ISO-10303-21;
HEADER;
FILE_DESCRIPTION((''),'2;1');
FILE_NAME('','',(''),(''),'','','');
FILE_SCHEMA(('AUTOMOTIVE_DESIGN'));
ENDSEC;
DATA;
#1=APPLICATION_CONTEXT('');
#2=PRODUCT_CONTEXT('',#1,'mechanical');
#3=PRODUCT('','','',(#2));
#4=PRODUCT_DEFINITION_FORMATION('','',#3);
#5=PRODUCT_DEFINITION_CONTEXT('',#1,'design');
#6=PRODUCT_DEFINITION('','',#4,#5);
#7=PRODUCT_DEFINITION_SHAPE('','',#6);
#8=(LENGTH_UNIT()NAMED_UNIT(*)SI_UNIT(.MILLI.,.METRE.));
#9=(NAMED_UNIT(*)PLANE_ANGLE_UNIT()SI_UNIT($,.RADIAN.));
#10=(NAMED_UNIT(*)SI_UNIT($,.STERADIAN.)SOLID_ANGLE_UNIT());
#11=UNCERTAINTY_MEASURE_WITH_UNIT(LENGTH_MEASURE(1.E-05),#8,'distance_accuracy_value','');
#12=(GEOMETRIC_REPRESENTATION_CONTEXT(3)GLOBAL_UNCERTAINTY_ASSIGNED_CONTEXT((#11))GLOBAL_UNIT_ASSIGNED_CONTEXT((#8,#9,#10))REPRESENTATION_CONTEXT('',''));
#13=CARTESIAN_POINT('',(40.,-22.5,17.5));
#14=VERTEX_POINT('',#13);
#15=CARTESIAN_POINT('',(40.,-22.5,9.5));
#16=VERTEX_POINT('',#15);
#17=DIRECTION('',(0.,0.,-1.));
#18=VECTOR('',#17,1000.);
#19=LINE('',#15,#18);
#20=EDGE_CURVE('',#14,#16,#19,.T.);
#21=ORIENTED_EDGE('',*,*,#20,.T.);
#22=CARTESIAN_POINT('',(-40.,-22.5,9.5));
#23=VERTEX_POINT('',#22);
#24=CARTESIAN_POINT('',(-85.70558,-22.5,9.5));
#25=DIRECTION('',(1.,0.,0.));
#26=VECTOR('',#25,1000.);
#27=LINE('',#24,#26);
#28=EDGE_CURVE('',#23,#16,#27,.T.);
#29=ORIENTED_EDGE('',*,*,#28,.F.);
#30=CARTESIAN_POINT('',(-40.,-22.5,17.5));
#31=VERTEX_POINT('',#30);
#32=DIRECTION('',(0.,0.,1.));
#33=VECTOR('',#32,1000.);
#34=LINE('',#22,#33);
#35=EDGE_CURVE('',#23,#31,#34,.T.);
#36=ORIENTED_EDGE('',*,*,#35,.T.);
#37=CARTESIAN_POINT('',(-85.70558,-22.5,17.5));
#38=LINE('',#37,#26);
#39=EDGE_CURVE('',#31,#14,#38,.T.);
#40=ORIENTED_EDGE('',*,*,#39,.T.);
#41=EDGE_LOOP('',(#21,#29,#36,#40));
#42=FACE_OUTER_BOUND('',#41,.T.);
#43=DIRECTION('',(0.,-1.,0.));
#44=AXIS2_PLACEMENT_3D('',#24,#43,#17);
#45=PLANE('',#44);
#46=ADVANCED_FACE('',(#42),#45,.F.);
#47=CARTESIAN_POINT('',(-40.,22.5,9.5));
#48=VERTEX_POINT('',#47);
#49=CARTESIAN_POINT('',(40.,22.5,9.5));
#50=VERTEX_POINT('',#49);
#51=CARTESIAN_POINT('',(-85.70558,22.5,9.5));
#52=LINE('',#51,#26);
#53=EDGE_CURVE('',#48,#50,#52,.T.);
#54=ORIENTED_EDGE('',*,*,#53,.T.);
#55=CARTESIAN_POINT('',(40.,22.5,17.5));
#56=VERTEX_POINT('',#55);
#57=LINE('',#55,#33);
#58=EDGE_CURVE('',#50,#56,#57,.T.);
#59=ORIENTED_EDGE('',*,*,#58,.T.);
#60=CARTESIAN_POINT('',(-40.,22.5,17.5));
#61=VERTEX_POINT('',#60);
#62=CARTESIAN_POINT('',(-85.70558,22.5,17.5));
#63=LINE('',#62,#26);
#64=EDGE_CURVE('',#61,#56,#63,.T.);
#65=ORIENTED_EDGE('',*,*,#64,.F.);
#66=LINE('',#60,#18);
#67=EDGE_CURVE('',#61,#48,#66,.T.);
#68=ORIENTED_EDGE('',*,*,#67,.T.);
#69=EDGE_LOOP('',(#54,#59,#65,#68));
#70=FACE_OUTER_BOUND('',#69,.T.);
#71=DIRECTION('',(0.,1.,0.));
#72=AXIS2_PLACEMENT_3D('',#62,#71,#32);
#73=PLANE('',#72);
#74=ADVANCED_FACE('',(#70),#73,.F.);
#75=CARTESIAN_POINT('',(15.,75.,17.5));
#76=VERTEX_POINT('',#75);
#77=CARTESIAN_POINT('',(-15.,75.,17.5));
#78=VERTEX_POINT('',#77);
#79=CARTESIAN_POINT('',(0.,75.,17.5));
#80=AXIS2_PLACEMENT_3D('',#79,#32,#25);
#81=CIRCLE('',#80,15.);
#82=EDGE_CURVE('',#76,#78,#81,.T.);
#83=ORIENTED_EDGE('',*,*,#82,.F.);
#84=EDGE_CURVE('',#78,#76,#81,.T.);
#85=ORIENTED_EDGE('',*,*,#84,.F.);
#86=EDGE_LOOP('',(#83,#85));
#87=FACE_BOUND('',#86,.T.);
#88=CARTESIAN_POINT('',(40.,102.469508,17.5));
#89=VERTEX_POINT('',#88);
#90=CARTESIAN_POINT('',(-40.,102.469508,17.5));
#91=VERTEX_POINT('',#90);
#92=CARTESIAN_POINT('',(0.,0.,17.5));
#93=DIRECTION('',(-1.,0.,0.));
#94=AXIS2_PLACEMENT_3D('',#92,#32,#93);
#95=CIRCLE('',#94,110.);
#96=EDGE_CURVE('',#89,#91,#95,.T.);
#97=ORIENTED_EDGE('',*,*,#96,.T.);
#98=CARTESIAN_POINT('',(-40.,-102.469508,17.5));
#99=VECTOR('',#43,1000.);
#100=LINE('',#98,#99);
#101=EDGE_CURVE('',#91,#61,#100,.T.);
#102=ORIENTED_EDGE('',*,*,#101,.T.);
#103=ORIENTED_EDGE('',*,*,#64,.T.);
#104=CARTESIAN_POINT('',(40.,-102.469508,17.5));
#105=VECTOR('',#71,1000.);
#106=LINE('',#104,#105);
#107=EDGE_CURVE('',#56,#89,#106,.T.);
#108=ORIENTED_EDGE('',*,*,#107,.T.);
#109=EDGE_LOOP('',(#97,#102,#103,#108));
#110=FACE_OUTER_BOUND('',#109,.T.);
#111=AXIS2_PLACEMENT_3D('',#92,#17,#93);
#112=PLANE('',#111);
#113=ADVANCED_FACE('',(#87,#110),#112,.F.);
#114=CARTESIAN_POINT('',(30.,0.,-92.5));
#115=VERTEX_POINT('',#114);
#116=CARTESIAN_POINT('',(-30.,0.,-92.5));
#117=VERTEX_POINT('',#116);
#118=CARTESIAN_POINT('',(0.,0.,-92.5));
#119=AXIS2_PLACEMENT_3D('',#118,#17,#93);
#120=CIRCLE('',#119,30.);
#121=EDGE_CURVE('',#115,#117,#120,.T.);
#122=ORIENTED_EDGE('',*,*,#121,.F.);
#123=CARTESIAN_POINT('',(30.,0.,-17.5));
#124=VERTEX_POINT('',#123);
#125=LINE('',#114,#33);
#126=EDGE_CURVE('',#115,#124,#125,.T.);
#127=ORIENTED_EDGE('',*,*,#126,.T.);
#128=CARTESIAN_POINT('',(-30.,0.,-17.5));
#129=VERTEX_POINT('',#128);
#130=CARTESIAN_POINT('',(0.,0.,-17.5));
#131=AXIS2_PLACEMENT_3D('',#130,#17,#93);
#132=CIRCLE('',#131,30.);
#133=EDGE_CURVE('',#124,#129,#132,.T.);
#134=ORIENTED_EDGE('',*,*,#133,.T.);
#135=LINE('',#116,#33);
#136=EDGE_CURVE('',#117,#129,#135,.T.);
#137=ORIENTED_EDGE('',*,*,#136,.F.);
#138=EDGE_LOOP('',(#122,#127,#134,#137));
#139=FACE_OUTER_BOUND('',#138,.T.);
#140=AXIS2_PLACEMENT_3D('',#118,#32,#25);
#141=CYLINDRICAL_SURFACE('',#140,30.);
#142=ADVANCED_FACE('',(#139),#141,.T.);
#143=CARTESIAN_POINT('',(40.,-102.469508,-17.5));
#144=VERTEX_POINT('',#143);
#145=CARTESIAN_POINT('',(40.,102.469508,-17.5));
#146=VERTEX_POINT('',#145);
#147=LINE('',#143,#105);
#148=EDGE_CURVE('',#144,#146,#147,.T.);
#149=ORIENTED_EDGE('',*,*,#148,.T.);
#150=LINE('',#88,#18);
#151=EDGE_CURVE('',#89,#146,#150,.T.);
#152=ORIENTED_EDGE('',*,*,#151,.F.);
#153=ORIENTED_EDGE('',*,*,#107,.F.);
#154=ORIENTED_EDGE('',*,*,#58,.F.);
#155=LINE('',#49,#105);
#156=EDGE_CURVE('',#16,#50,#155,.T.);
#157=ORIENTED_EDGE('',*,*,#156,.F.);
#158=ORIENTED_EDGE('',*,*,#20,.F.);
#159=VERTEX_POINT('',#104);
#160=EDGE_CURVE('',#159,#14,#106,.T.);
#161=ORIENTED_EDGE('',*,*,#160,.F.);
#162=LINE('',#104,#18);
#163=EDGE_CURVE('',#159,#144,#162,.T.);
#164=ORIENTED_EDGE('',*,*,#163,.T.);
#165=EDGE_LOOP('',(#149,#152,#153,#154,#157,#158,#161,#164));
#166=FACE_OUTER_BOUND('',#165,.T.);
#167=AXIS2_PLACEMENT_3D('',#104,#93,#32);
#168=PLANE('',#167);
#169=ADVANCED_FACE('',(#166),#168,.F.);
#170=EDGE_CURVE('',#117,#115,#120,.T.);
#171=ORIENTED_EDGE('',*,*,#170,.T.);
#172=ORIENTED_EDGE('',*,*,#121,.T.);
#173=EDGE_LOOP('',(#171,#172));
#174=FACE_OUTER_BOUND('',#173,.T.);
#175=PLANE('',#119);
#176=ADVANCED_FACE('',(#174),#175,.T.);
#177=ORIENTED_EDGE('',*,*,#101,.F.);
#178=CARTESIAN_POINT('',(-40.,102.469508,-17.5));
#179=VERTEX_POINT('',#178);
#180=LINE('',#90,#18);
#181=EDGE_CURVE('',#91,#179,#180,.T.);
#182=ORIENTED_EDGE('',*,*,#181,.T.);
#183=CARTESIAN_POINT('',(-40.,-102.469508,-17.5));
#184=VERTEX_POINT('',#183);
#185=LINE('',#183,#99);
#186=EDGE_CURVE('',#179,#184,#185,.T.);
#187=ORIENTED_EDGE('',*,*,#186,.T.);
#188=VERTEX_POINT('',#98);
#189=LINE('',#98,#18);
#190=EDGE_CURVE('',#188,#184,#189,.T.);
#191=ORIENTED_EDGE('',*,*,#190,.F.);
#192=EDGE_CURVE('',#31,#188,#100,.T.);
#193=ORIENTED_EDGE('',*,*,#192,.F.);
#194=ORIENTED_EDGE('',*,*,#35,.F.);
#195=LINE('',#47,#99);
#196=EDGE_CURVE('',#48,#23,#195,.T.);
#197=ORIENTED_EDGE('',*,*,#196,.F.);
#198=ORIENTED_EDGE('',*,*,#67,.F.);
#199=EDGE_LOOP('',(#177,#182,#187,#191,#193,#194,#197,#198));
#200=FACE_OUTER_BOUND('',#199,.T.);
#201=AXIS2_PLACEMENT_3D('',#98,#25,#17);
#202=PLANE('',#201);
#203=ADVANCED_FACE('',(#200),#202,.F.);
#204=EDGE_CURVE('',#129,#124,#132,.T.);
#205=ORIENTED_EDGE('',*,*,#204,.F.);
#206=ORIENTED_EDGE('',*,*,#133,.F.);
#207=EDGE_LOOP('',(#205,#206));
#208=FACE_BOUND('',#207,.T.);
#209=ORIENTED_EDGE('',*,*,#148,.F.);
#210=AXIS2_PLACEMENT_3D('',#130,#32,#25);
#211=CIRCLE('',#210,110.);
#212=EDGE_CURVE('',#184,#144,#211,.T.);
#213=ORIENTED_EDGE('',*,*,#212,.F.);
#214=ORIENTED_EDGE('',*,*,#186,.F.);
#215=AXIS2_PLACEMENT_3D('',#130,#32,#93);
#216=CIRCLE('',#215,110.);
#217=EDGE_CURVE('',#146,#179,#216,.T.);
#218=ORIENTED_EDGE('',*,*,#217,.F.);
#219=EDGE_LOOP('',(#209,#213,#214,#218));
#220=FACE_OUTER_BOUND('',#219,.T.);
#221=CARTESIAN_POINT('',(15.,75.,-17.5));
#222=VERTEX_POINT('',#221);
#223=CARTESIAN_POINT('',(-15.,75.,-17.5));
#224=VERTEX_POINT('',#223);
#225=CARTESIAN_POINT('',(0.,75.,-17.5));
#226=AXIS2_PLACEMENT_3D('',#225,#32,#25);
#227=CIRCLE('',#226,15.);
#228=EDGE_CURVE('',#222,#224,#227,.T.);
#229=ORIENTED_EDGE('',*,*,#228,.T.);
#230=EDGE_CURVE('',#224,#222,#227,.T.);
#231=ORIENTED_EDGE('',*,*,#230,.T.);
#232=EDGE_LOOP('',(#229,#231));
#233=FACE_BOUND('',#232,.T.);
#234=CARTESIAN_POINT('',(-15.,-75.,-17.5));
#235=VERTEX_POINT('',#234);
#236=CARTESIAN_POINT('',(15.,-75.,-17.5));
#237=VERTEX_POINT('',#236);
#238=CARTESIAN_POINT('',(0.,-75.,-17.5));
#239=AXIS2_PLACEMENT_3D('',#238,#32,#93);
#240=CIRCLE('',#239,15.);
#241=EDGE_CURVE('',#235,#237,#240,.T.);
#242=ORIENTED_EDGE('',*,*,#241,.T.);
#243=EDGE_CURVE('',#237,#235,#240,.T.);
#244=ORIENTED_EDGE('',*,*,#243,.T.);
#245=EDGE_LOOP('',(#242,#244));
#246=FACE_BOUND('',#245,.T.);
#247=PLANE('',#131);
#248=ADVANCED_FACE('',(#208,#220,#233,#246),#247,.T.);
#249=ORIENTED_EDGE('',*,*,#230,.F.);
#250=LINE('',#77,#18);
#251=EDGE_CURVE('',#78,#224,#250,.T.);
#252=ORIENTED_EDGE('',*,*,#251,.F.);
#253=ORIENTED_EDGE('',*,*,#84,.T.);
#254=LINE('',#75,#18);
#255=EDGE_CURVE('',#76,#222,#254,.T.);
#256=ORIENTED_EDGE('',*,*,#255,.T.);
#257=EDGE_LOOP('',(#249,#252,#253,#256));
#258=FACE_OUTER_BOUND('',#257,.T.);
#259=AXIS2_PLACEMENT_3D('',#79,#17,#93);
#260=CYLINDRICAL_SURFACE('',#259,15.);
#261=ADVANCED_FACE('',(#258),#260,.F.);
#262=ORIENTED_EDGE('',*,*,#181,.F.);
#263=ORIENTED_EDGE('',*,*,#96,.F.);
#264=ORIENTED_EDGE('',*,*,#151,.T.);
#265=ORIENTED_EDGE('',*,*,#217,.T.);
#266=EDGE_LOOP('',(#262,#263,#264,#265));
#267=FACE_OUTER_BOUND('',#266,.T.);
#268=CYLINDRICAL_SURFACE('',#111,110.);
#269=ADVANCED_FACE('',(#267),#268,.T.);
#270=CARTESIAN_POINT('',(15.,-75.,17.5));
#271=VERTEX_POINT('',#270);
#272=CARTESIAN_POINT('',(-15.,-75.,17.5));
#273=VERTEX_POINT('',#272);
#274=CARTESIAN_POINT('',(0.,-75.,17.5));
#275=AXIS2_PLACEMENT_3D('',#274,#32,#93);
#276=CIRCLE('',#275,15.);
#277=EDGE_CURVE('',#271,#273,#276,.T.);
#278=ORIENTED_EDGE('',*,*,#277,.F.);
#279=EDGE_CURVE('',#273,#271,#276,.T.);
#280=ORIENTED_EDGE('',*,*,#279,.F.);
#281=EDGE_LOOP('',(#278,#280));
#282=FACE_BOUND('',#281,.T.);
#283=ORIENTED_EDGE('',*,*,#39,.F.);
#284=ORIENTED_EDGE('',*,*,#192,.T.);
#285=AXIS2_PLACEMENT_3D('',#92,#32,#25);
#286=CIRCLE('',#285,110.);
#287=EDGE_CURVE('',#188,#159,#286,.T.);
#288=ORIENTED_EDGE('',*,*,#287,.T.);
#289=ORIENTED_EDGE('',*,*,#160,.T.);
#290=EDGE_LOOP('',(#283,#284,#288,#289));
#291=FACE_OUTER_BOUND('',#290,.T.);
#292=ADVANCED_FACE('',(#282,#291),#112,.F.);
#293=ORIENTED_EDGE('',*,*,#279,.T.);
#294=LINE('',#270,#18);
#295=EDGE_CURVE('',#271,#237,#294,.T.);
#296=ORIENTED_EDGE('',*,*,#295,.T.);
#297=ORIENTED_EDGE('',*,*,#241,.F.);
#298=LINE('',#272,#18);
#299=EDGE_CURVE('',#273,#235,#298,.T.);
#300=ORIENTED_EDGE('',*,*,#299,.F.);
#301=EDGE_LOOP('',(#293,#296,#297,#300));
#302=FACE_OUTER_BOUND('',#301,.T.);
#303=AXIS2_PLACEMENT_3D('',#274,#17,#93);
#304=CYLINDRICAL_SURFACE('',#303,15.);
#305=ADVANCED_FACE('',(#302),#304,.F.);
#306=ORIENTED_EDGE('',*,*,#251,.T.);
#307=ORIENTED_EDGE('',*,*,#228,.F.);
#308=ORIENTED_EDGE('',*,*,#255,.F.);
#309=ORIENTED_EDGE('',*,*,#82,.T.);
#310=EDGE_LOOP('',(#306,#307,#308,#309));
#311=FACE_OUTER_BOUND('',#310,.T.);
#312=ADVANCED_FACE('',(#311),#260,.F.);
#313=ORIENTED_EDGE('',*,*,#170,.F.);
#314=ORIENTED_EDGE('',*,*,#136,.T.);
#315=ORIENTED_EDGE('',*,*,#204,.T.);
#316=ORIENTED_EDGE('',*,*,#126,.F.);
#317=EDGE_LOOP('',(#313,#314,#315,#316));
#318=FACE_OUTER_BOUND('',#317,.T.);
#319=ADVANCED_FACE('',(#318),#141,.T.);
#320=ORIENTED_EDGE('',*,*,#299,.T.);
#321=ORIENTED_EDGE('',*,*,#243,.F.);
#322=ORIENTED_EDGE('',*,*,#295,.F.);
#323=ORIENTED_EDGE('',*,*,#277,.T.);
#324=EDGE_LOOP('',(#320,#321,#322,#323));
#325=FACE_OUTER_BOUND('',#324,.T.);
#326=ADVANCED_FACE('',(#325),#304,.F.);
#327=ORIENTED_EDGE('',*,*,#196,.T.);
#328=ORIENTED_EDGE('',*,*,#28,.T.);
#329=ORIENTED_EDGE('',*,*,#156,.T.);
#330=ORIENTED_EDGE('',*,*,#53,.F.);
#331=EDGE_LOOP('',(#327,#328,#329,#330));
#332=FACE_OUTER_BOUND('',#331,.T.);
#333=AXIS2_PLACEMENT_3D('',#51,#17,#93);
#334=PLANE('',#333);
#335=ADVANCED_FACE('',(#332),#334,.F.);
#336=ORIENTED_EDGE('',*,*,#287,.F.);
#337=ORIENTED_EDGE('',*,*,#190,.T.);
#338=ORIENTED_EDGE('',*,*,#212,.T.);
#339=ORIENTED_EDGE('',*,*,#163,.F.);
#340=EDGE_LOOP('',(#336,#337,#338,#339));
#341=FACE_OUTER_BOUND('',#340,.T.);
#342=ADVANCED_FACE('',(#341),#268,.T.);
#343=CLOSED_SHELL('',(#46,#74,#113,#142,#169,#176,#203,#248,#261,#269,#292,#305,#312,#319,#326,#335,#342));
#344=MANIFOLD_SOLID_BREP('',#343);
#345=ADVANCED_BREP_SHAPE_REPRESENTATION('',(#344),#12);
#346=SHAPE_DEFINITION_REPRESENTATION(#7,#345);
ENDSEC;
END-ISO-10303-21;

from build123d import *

# Parameters (mm, degrees)
PLATE_PROFILE_SKETCH_R    = 15
KEEPER_PLATE_BODY_DEPTH   = 17.5
MOUNTING_HOLES_SKETCH_W   = 8
MOUNTING_HOLES_SKETCH_H   = 45
MOUNTING_HOLES_DEPTH      = 80
BOSS_60_SKETCH_R          = 30
CYLINDRICAL_BOSS_60_DEPTH = 75


with BuildPart() as part:
    # Plate Profile Sketch → Keeper Plate Body (new, symmetric)
    with BuildSketch(Plane.XY):
        with BuildLine():
            Line((-40, -102.46950766), (-40, 102.46950766))
            ThreePointArc((-40, 102.46950766), (0, 110), (40, 102.46950766))
            Line((40, 102.46950766), (40, -102.46950766))
            ThreePointArc((40, -102.46950766), (0, -110), (-40, -102.46950766))
        make_face()
        with Locations((0, 75)):
            Circle(PLATE_PROFILE_SKETCH_R, mode=Mode.SUBTRACT)
        with Locations(Location((0, -75, 0), (0, 0, 180))):
            Circle(PLATE_PROFILE_SKETCH_R, mode=Mode.SUBTRACT)
    extrude(amount=KEEPER_PLATE_BODY_DEPTH, both=True)

    # Mounting Holes Sketch → Mounting Holes (cut)
    with BuildSketch(Plane(origin=(40, 0, 0), x_dir=(0, 0, -1), z_dir=(1, 0, 0))):
        with Locations((-13.5, 0)):
            Rectangle(MOUNTING_HOLES_SKETCH_W, MOUNTING_HOLES_SKETCH_H)
    extrude(amount=-MOUNTING_HOLES_DEPTH, mode=Mode.SUBTRACT)

    # Boss Ø60 Sketch → Cylindrical Boss Ø60 (add)
    with BuildSketch(Plane(origin=(0, 0, -17.5), x_dir=(-1, 0, 0), z_dir=(0, 0, -1))):
        Circle(BOSS_60_SKETCH_R)
    extrude(amount=CYLINDRICAL_BOSS_60_DEPTH)


solid = part.part
